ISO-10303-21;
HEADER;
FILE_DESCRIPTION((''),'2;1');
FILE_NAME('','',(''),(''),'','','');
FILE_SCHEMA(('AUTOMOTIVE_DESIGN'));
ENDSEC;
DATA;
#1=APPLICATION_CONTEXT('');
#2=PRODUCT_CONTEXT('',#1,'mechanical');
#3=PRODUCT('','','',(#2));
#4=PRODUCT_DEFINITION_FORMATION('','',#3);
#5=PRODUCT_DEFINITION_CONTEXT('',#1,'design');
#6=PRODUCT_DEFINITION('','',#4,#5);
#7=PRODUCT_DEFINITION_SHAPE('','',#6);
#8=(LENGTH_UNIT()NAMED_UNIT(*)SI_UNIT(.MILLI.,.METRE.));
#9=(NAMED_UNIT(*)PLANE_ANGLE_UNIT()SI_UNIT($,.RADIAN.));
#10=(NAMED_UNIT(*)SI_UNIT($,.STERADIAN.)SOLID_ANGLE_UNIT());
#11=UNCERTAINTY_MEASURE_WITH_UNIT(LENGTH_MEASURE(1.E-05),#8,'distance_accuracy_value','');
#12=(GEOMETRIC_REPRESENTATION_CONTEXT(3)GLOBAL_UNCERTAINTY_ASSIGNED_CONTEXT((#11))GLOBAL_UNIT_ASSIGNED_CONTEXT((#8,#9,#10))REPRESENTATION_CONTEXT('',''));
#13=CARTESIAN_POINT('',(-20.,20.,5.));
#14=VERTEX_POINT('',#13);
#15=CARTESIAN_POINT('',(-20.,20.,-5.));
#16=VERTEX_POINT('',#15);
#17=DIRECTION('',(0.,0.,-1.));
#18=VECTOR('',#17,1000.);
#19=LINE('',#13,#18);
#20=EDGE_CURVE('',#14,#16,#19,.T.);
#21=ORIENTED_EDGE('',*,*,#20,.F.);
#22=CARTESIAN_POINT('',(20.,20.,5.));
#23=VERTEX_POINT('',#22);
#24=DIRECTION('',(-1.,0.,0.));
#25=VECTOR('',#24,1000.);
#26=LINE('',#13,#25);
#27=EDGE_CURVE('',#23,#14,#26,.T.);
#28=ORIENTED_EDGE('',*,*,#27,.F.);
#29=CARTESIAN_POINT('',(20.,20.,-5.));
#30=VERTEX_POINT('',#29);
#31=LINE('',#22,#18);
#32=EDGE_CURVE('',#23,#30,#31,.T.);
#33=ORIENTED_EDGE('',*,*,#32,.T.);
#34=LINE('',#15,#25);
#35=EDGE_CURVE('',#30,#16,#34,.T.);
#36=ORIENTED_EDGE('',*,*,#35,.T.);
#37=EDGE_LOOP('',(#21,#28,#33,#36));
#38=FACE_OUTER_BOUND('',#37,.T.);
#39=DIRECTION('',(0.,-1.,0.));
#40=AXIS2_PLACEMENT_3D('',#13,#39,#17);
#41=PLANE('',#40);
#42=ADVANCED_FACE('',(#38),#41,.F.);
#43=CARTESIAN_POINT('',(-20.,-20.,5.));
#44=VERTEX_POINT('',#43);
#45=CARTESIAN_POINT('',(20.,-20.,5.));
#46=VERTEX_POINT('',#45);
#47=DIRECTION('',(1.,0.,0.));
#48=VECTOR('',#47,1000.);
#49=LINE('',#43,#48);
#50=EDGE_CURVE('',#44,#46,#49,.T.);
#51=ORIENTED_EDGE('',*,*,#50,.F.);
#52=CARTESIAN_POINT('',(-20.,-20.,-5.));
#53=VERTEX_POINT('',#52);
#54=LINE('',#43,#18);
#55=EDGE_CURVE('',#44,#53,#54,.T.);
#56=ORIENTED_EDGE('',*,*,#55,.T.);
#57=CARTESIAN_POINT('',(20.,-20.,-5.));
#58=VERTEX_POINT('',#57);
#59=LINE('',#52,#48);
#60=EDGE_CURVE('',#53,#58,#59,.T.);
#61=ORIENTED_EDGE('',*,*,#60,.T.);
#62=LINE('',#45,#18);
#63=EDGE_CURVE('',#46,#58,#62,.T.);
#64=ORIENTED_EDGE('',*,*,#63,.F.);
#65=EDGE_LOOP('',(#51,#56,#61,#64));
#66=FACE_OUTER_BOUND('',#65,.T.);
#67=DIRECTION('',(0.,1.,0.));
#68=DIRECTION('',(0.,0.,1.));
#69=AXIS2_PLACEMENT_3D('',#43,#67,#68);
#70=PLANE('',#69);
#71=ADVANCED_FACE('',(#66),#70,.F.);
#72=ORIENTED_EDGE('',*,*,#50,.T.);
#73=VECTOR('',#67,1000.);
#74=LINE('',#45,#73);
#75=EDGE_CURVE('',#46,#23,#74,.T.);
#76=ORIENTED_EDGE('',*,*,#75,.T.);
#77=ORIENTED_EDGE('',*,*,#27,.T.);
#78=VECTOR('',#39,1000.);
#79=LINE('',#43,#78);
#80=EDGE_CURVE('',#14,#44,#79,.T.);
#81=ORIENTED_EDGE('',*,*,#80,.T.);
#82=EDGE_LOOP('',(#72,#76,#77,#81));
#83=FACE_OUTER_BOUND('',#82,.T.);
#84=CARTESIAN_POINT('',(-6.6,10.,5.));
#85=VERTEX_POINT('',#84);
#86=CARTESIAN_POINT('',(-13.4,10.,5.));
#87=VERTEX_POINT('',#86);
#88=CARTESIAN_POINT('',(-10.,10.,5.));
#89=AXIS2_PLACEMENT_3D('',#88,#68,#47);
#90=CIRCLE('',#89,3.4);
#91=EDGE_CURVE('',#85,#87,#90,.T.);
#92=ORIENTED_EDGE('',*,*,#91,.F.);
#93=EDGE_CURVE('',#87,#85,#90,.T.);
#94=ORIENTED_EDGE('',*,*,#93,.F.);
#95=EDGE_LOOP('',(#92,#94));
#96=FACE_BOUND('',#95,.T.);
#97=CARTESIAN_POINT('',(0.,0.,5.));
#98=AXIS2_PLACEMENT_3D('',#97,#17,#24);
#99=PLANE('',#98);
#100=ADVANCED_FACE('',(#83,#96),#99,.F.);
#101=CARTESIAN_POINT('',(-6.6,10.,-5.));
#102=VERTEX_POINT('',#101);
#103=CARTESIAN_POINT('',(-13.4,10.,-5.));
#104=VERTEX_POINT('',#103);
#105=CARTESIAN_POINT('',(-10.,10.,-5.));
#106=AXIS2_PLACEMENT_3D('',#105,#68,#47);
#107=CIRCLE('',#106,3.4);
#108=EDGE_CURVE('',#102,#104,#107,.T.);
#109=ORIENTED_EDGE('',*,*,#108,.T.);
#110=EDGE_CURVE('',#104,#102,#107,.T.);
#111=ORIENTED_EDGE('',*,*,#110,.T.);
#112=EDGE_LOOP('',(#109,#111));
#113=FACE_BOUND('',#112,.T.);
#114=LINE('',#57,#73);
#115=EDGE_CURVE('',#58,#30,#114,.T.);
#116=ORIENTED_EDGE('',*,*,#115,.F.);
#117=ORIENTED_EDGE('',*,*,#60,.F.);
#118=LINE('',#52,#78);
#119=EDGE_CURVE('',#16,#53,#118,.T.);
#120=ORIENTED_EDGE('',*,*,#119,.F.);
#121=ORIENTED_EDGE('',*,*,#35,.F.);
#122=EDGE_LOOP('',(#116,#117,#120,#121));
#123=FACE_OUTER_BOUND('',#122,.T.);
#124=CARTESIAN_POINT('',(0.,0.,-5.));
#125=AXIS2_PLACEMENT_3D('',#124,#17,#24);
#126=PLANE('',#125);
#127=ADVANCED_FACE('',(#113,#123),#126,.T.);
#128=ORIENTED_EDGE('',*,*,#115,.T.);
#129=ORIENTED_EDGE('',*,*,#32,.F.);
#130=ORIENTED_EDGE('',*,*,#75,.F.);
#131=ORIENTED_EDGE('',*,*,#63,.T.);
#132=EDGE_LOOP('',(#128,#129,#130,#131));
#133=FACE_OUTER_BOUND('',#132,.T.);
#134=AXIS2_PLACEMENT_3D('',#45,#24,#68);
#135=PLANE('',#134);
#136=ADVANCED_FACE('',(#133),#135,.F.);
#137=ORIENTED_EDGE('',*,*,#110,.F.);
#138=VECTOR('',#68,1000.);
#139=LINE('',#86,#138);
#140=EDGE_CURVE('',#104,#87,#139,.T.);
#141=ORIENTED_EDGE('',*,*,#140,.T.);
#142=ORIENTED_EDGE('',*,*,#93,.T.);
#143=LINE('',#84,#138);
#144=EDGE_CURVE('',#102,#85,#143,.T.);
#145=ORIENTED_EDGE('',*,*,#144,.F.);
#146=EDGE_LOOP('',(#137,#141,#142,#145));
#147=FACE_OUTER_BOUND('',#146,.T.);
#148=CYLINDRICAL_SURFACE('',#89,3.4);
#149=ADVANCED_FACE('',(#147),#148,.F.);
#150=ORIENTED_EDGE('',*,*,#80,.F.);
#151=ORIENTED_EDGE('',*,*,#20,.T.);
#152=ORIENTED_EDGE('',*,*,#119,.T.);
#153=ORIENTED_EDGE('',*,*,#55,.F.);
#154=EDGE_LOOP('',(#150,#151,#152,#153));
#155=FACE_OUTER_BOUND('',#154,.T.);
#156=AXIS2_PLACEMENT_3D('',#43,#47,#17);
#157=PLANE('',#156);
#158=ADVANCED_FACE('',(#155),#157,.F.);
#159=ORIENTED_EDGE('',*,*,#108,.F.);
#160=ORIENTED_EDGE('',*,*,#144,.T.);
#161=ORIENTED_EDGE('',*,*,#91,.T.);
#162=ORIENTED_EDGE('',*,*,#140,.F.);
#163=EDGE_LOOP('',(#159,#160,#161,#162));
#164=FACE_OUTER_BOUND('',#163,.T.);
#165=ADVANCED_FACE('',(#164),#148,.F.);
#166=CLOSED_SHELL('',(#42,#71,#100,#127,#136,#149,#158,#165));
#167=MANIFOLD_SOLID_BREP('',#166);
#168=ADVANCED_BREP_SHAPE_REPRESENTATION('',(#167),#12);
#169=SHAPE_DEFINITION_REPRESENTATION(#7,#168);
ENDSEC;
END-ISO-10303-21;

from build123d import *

# Parameters (mm, degrees)
SKETCH_1_W         = 40
SKETCH_1_H         = 40
EXTRUDE_1_DEPTH    = 5
HOLE_WIZARD_M8_1_D = 6.8


with BuildPart() as part:
    # 草图1 → 凸台-拉伸1 (new, symmetric)
    with BuildSketch(Plane.XY):
        Rectangle(SKETCH_1_W, SKETCH_1_H)
    extrude(amount=EXTRUDE_1_DEPTH, both=True)

    # M8 螺纹孔1 (through all)
    with Locations(Plane.XY.offset(5)):
        with Locations((-10, 10)):
            Hole(HOLE_WIZARD_M8_1_D / 2)


solid = part.part
